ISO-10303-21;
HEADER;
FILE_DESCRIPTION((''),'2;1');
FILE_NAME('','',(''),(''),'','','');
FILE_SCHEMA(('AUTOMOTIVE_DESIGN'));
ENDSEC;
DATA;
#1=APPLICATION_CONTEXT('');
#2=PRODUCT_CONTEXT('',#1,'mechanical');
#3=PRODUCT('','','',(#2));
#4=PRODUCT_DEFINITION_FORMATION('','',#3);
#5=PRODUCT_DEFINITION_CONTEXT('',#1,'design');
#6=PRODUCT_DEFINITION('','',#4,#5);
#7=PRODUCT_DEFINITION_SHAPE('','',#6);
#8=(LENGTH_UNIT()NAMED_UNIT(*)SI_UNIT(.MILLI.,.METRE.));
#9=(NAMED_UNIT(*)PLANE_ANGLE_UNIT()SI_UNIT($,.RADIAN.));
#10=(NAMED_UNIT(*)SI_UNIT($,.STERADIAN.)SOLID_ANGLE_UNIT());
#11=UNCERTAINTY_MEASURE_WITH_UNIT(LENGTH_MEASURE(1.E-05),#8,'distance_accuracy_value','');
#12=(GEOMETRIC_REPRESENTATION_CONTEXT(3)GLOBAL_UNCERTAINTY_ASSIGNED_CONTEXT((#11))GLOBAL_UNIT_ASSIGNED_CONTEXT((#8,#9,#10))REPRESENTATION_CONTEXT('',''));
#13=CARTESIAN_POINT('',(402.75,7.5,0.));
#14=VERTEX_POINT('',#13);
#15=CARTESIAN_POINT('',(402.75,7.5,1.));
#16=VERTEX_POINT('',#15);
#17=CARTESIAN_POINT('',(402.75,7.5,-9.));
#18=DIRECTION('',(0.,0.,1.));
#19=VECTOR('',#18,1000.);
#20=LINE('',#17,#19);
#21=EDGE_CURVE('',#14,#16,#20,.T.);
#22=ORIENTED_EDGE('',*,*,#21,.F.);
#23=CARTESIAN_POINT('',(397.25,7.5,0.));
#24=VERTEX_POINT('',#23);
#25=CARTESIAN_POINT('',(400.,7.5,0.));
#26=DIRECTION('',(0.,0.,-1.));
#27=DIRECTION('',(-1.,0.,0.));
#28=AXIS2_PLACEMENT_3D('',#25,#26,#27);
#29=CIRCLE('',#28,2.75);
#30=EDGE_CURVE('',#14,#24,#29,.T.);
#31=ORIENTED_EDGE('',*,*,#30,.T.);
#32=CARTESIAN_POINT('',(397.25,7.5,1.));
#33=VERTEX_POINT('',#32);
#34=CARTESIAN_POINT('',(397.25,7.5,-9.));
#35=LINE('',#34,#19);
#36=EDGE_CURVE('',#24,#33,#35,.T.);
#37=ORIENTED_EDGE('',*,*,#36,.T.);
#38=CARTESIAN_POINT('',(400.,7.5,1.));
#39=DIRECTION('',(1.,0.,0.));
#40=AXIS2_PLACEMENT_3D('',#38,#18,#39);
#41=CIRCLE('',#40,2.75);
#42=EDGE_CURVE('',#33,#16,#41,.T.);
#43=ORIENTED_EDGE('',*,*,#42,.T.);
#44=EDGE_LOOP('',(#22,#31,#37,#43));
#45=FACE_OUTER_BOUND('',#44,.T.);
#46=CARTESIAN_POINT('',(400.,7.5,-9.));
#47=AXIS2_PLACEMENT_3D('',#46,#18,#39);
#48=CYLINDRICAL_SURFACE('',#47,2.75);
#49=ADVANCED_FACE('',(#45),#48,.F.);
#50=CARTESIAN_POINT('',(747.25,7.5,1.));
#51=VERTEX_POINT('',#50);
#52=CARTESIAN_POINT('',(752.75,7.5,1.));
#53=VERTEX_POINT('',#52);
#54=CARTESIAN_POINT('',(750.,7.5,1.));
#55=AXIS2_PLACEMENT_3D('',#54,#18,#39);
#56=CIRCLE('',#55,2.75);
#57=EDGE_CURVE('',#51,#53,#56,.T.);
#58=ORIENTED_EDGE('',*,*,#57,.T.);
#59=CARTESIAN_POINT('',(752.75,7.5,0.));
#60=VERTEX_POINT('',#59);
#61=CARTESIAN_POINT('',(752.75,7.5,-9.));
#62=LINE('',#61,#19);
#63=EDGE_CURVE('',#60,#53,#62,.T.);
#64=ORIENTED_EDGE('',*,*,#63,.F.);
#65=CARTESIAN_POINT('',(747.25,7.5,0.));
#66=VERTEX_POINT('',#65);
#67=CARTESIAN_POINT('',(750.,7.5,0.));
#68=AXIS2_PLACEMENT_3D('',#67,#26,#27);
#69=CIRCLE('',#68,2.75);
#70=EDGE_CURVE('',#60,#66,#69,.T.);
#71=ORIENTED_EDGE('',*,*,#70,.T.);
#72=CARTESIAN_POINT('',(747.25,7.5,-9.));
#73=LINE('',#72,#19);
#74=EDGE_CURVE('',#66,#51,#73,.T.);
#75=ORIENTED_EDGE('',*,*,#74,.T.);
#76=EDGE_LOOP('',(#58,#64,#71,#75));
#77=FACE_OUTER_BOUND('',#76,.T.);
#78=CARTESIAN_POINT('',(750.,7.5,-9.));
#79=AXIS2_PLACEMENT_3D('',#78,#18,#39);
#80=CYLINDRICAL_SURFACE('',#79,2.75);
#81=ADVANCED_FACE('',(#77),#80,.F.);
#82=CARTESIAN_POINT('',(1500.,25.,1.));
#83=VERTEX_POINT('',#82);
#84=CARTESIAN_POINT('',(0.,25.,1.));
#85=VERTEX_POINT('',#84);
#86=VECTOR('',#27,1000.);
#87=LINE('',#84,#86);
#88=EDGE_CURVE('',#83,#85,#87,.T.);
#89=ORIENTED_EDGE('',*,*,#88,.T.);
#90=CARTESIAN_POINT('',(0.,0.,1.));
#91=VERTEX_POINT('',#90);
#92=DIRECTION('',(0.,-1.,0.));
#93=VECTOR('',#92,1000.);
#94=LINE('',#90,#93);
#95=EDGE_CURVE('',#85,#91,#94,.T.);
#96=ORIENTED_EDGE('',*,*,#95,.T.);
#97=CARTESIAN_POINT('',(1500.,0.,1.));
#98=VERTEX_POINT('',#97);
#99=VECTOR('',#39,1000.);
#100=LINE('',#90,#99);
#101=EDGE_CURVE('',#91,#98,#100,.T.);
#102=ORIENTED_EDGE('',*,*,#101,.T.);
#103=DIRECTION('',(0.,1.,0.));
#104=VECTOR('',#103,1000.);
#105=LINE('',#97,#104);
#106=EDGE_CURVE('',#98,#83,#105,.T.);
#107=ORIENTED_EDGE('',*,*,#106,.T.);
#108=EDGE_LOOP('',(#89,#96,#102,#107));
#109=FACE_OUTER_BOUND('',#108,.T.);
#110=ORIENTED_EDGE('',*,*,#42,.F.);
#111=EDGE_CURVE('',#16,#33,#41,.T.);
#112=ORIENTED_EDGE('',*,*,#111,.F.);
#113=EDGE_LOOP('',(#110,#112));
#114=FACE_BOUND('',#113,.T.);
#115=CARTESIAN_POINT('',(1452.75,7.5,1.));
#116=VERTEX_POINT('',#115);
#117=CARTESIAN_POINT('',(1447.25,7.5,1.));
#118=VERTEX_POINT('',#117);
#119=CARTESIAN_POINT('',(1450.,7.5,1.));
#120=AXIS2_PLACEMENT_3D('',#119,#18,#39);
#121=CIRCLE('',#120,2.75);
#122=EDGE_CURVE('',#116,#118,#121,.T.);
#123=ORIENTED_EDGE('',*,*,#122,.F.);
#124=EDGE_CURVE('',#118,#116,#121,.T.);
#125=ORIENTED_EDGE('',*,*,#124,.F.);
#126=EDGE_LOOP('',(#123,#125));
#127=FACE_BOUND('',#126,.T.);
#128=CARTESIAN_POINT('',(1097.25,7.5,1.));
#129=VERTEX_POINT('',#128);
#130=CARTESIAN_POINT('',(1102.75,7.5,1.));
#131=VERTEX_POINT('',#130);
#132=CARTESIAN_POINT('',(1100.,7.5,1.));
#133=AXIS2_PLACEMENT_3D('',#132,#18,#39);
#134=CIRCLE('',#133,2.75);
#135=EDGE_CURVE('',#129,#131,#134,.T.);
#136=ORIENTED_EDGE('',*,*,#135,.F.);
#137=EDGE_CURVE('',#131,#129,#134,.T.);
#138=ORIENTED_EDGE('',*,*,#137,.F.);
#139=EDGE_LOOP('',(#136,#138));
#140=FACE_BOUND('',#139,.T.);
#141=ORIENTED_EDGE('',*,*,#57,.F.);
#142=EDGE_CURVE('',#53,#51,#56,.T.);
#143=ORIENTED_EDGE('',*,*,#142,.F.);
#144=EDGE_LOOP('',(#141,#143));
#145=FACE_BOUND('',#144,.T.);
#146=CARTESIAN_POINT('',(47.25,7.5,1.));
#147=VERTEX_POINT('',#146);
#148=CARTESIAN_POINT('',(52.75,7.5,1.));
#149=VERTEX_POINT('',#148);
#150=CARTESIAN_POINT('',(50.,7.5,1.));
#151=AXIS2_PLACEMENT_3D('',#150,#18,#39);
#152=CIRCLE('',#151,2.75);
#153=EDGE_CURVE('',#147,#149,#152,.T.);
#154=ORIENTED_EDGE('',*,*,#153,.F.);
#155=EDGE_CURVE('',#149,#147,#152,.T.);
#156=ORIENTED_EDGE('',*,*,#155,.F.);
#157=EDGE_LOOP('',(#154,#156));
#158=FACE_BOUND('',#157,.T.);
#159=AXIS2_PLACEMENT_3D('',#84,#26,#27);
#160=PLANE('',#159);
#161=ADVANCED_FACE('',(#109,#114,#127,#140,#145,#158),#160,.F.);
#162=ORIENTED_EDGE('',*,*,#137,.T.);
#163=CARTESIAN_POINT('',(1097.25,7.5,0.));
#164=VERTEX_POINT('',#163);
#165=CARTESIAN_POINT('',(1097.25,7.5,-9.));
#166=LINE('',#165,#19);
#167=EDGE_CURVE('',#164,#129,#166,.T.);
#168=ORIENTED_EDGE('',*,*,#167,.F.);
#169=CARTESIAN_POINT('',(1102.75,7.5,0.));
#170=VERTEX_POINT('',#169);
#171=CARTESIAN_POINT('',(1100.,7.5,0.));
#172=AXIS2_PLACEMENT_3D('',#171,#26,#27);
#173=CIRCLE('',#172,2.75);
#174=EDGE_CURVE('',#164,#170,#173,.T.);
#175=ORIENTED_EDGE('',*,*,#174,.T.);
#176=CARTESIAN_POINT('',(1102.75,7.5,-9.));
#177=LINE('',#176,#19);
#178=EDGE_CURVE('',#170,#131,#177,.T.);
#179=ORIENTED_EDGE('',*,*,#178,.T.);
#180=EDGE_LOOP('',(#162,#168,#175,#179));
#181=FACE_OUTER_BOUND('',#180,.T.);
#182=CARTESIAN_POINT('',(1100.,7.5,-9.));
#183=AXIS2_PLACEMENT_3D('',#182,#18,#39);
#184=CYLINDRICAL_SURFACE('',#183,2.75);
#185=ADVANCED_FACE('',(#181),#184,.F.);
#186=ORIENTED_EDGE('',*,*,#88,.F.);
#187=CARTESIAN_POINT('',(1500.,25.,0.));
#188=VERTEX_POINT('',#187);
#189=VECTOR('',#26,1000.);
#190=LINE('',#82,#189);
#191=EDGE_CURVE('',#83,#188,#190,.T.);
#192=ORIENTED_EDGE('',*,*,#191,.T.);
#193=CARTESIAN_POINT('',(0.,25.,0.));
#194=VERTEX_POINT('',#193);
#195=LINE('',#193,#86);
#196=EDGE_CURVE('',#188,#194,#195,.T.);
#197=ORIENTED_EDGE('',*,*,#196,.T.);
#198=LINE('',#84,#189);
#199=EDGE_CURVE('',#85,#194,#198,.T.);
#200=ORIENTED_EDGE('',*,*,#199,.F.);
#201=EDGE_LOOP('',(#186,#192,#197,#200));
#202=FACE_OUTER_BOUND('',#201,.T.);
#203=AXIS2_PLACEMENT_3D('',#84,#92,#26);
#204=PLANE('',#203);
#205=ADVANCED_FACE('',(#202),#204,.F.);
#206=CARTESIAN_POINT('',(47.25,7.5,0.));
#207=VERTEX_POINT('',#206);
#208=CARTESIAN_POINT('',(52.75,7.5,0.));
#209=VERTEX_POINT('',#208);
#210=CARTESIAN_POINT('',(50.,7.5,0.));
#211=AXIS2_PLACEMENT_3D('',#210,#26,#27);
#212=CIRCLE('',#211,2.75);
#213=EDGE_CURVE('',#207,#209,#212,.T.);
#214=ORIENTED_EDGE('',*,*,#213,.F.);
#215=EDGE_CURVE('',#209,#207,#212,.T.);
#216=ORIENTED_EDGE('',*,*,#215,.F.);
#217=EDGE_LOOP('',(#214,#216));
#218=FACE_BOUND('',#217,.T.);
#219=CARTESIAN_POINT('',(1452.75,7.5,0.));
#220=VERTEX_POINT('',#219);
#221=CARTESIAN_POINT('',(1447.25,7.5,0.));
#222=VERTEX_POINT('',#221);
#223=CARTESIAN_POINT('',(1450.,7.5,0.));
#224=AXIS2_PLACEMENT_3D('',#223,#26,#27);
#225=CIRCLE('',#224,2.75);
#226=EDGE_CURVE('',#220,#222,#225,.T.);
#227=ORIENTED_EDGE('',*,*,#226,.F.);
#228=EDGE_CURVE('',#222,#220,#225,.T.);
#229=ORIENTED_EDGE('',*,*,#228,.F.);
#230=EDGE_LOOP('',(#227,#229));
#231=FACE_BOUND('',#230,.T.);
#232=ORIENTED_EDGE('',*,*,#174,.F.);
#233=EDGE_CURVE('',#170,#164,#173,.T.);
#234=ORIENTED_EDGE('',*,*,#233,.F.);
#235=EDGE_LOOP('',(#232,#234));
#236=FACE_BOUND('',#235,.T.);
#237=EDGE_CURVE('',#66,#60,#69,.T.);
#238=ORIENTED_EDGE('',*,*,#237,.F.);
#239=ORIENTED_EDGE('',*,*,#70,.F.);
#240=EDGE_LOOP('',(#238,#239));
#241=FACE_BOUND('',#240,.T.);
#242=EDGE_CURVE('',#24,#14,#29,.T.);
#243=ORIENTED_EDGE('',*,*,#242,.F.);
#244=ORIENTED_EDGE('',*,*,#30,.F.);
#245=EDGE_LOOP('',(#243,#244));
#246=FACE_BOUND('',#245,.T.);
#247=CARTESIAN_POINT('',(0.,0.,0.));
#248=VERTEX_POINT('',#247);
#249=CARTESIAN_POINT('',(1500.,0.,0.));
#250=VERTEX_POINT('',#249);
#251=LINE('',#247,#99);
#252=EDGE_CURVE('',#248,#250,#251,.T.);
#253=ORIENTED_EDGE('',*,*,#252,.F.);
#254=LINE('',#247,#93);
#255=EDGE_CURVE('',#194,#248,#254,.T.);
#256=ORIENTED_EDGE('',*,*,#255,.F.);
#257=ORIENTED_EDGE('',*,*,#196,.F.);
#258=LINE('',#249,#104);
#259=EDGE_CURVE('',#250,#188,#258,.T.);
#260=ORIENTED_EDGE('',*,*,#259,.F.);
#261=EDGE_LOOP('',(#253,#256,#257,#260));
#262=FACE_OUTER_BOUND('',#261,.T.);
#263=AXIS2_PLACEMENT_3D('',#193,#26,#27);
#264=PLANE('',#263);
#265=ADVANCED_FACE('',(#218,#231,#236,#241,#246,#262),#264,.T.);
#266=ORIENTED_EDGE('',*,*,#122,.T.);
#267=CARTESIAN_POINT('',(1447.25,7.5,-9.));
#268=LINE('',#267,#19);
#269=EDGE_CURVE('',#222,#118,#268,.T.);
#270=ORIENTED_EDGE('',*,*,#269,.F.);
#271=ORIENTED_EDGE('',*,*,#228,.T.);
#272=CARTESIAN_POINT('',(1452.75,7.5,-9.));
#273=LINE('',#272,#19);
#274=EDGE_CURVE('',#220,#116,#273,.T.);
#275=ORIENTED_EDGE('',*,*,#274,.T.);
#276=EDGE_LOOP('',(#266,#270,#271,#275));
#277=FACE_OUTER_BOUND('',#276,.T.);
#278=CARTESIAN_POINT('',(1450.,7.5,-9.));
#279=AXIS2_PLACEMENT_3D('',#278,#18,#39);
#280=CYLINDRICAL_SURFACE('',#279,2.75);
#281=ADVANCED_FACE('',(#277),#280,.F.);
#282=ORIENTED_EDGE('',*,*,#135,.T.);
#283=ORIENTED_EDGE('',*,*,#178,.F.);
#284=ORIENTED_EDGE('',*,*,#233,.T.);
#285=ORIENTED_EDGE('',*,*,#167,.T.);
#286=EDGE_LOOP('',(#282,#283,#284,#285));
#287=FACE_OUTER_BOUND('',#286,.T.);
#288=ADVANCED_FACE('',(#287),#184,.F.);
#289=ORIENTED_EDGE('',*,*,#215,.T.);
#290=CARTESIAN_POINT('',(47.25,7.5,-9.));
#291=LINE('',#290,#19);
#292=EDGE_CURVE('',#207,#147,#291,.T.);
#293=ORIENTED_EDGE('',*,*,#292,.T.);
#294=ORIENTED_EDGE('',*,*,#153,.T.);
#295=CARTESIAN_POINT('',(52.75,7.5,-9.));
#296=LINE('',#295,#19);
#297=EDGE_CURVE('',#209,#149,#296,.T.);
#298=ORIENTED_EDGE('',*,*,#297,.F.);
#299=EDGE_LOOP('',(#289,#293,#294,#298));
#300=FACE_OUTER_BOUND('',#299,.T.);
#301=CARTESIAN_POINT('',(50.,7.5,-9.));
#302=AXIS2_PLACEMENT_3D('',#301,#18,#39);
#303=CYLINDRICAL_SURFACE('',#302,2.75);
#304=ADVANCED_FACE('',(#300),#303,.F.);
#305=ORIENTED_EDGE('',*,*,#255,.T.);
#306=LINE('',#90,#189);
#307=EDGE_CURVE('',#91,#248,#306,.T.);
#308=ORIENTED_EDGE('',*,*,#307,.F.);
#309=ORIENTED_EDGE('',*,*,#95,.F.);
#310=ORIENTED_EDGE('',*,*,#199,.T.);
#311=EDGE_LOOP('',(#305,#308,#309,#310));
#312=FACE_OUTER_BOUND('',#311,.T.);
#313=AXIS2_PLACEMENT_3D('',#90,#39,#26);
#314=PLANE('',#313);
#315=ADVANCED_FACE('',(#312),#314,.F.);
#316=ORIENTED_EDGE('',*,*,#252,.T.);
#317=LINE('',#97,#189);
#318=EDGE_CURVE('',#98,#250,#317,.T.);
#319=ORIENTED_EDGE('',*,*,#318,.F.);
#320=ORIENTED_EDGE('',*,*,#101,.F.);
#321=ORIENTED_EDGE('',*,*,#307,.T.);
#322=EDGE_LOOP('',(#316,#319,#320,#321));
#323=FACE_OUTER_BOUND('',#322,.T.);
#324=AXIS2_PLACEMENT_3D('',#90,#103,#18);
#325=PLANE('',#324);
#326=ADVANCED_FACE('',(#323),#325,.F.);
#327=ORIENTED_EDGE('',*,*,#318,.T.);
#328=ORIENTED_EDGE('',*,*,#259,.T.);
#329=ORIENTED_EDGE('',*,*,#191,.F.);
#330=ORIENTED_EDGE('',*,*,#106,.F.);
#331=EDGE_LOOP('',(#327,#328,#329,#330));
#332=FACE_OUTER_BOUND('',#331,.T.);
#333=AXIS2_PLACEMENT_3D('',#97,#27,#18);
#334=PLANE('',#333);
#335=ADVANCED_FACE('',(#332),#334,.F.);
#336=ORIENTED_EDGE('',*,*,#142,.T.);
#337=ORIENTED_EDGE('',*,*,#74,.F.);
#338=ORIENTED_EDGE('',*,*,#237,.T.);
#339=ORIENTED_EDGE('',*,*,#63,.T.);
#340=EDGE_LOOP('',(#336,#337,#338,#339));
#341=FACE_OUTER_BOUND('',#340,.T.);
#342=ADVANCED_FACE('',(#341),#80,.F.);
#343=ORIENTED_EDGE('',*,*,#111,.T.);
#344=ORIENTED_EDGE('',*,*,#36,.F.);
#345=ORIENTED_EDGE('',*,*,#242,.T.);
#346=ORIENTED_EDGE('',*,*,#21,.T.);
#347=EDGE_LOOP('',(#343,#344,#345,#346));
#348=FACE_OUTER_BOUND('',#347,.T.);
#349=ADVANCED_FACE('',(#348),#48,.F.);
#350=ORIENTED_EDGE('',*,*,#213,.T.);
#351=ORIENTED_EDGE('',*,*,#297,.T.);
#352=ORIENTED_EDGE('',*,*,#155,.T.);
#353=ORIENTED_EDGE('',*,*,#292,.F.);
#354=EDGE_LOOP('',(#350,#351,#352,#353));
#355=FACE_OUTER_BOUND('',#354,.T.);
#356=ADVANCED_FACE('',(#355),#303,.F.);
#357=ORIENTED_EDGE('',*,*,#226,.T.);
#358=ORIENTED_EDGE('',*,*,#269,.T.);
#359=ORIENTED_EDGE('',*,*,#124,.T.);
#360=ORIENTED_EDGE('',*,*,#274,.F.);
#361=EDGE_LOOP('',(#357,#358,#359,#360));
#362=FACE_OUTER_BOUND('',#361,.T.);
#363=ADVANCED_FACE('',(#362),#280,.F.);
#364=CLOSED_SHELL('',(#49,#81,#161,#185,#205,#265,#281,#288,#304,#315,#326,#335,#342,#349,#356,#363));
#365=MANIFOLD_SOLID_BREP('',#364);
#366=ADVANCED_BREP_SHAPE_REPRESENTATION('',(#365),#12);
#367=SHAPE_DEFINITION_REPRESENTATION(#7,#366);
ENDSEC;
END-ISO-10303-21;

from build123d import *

# Parameters (mm, degrees)
SKETCH_1_W          = 1500
SKETCH_1_H          = 25
EXTRUDE_1_DEPTH     = 1
SKETCH_2_R          = 2.75
CUT_EXTRUDE_1_DEPTH = 10


with BuildPart() as part:
    # 草图1 → 凸台-拉伸1 (new body)
    with BuildSketch(Plane.XY):
        with Locations((750, 12.5)):
            Rectangle(SKETCH_1_W, SKETCH_1_H)
    extrude(amount=EXTRUDE_1_DEPTH)

    # 草图2 → 切除-拉伸1 (cut)
    with BuildSketch(Plane.XY.offset(1)):
        with Locations((50, 7.5)):
            Circle(SKETCH_2_R)
        with Locations((400, 7.5)):
            Circle(SKETCH_2_R)
        with Locations((750, 7.5)):
            Circle(SKETCH_2_R)
        with Locations((1100, 7.5)):
            Circle(SKETCH_2_R)
        with Locations((1450, 7.5)):
            Circle(SKETCH_2_R)
    extrude(amount=-CUT_EXTRUDE_1_DEPTH, mode=Mode.SUBTRACT)


solid = part.part
